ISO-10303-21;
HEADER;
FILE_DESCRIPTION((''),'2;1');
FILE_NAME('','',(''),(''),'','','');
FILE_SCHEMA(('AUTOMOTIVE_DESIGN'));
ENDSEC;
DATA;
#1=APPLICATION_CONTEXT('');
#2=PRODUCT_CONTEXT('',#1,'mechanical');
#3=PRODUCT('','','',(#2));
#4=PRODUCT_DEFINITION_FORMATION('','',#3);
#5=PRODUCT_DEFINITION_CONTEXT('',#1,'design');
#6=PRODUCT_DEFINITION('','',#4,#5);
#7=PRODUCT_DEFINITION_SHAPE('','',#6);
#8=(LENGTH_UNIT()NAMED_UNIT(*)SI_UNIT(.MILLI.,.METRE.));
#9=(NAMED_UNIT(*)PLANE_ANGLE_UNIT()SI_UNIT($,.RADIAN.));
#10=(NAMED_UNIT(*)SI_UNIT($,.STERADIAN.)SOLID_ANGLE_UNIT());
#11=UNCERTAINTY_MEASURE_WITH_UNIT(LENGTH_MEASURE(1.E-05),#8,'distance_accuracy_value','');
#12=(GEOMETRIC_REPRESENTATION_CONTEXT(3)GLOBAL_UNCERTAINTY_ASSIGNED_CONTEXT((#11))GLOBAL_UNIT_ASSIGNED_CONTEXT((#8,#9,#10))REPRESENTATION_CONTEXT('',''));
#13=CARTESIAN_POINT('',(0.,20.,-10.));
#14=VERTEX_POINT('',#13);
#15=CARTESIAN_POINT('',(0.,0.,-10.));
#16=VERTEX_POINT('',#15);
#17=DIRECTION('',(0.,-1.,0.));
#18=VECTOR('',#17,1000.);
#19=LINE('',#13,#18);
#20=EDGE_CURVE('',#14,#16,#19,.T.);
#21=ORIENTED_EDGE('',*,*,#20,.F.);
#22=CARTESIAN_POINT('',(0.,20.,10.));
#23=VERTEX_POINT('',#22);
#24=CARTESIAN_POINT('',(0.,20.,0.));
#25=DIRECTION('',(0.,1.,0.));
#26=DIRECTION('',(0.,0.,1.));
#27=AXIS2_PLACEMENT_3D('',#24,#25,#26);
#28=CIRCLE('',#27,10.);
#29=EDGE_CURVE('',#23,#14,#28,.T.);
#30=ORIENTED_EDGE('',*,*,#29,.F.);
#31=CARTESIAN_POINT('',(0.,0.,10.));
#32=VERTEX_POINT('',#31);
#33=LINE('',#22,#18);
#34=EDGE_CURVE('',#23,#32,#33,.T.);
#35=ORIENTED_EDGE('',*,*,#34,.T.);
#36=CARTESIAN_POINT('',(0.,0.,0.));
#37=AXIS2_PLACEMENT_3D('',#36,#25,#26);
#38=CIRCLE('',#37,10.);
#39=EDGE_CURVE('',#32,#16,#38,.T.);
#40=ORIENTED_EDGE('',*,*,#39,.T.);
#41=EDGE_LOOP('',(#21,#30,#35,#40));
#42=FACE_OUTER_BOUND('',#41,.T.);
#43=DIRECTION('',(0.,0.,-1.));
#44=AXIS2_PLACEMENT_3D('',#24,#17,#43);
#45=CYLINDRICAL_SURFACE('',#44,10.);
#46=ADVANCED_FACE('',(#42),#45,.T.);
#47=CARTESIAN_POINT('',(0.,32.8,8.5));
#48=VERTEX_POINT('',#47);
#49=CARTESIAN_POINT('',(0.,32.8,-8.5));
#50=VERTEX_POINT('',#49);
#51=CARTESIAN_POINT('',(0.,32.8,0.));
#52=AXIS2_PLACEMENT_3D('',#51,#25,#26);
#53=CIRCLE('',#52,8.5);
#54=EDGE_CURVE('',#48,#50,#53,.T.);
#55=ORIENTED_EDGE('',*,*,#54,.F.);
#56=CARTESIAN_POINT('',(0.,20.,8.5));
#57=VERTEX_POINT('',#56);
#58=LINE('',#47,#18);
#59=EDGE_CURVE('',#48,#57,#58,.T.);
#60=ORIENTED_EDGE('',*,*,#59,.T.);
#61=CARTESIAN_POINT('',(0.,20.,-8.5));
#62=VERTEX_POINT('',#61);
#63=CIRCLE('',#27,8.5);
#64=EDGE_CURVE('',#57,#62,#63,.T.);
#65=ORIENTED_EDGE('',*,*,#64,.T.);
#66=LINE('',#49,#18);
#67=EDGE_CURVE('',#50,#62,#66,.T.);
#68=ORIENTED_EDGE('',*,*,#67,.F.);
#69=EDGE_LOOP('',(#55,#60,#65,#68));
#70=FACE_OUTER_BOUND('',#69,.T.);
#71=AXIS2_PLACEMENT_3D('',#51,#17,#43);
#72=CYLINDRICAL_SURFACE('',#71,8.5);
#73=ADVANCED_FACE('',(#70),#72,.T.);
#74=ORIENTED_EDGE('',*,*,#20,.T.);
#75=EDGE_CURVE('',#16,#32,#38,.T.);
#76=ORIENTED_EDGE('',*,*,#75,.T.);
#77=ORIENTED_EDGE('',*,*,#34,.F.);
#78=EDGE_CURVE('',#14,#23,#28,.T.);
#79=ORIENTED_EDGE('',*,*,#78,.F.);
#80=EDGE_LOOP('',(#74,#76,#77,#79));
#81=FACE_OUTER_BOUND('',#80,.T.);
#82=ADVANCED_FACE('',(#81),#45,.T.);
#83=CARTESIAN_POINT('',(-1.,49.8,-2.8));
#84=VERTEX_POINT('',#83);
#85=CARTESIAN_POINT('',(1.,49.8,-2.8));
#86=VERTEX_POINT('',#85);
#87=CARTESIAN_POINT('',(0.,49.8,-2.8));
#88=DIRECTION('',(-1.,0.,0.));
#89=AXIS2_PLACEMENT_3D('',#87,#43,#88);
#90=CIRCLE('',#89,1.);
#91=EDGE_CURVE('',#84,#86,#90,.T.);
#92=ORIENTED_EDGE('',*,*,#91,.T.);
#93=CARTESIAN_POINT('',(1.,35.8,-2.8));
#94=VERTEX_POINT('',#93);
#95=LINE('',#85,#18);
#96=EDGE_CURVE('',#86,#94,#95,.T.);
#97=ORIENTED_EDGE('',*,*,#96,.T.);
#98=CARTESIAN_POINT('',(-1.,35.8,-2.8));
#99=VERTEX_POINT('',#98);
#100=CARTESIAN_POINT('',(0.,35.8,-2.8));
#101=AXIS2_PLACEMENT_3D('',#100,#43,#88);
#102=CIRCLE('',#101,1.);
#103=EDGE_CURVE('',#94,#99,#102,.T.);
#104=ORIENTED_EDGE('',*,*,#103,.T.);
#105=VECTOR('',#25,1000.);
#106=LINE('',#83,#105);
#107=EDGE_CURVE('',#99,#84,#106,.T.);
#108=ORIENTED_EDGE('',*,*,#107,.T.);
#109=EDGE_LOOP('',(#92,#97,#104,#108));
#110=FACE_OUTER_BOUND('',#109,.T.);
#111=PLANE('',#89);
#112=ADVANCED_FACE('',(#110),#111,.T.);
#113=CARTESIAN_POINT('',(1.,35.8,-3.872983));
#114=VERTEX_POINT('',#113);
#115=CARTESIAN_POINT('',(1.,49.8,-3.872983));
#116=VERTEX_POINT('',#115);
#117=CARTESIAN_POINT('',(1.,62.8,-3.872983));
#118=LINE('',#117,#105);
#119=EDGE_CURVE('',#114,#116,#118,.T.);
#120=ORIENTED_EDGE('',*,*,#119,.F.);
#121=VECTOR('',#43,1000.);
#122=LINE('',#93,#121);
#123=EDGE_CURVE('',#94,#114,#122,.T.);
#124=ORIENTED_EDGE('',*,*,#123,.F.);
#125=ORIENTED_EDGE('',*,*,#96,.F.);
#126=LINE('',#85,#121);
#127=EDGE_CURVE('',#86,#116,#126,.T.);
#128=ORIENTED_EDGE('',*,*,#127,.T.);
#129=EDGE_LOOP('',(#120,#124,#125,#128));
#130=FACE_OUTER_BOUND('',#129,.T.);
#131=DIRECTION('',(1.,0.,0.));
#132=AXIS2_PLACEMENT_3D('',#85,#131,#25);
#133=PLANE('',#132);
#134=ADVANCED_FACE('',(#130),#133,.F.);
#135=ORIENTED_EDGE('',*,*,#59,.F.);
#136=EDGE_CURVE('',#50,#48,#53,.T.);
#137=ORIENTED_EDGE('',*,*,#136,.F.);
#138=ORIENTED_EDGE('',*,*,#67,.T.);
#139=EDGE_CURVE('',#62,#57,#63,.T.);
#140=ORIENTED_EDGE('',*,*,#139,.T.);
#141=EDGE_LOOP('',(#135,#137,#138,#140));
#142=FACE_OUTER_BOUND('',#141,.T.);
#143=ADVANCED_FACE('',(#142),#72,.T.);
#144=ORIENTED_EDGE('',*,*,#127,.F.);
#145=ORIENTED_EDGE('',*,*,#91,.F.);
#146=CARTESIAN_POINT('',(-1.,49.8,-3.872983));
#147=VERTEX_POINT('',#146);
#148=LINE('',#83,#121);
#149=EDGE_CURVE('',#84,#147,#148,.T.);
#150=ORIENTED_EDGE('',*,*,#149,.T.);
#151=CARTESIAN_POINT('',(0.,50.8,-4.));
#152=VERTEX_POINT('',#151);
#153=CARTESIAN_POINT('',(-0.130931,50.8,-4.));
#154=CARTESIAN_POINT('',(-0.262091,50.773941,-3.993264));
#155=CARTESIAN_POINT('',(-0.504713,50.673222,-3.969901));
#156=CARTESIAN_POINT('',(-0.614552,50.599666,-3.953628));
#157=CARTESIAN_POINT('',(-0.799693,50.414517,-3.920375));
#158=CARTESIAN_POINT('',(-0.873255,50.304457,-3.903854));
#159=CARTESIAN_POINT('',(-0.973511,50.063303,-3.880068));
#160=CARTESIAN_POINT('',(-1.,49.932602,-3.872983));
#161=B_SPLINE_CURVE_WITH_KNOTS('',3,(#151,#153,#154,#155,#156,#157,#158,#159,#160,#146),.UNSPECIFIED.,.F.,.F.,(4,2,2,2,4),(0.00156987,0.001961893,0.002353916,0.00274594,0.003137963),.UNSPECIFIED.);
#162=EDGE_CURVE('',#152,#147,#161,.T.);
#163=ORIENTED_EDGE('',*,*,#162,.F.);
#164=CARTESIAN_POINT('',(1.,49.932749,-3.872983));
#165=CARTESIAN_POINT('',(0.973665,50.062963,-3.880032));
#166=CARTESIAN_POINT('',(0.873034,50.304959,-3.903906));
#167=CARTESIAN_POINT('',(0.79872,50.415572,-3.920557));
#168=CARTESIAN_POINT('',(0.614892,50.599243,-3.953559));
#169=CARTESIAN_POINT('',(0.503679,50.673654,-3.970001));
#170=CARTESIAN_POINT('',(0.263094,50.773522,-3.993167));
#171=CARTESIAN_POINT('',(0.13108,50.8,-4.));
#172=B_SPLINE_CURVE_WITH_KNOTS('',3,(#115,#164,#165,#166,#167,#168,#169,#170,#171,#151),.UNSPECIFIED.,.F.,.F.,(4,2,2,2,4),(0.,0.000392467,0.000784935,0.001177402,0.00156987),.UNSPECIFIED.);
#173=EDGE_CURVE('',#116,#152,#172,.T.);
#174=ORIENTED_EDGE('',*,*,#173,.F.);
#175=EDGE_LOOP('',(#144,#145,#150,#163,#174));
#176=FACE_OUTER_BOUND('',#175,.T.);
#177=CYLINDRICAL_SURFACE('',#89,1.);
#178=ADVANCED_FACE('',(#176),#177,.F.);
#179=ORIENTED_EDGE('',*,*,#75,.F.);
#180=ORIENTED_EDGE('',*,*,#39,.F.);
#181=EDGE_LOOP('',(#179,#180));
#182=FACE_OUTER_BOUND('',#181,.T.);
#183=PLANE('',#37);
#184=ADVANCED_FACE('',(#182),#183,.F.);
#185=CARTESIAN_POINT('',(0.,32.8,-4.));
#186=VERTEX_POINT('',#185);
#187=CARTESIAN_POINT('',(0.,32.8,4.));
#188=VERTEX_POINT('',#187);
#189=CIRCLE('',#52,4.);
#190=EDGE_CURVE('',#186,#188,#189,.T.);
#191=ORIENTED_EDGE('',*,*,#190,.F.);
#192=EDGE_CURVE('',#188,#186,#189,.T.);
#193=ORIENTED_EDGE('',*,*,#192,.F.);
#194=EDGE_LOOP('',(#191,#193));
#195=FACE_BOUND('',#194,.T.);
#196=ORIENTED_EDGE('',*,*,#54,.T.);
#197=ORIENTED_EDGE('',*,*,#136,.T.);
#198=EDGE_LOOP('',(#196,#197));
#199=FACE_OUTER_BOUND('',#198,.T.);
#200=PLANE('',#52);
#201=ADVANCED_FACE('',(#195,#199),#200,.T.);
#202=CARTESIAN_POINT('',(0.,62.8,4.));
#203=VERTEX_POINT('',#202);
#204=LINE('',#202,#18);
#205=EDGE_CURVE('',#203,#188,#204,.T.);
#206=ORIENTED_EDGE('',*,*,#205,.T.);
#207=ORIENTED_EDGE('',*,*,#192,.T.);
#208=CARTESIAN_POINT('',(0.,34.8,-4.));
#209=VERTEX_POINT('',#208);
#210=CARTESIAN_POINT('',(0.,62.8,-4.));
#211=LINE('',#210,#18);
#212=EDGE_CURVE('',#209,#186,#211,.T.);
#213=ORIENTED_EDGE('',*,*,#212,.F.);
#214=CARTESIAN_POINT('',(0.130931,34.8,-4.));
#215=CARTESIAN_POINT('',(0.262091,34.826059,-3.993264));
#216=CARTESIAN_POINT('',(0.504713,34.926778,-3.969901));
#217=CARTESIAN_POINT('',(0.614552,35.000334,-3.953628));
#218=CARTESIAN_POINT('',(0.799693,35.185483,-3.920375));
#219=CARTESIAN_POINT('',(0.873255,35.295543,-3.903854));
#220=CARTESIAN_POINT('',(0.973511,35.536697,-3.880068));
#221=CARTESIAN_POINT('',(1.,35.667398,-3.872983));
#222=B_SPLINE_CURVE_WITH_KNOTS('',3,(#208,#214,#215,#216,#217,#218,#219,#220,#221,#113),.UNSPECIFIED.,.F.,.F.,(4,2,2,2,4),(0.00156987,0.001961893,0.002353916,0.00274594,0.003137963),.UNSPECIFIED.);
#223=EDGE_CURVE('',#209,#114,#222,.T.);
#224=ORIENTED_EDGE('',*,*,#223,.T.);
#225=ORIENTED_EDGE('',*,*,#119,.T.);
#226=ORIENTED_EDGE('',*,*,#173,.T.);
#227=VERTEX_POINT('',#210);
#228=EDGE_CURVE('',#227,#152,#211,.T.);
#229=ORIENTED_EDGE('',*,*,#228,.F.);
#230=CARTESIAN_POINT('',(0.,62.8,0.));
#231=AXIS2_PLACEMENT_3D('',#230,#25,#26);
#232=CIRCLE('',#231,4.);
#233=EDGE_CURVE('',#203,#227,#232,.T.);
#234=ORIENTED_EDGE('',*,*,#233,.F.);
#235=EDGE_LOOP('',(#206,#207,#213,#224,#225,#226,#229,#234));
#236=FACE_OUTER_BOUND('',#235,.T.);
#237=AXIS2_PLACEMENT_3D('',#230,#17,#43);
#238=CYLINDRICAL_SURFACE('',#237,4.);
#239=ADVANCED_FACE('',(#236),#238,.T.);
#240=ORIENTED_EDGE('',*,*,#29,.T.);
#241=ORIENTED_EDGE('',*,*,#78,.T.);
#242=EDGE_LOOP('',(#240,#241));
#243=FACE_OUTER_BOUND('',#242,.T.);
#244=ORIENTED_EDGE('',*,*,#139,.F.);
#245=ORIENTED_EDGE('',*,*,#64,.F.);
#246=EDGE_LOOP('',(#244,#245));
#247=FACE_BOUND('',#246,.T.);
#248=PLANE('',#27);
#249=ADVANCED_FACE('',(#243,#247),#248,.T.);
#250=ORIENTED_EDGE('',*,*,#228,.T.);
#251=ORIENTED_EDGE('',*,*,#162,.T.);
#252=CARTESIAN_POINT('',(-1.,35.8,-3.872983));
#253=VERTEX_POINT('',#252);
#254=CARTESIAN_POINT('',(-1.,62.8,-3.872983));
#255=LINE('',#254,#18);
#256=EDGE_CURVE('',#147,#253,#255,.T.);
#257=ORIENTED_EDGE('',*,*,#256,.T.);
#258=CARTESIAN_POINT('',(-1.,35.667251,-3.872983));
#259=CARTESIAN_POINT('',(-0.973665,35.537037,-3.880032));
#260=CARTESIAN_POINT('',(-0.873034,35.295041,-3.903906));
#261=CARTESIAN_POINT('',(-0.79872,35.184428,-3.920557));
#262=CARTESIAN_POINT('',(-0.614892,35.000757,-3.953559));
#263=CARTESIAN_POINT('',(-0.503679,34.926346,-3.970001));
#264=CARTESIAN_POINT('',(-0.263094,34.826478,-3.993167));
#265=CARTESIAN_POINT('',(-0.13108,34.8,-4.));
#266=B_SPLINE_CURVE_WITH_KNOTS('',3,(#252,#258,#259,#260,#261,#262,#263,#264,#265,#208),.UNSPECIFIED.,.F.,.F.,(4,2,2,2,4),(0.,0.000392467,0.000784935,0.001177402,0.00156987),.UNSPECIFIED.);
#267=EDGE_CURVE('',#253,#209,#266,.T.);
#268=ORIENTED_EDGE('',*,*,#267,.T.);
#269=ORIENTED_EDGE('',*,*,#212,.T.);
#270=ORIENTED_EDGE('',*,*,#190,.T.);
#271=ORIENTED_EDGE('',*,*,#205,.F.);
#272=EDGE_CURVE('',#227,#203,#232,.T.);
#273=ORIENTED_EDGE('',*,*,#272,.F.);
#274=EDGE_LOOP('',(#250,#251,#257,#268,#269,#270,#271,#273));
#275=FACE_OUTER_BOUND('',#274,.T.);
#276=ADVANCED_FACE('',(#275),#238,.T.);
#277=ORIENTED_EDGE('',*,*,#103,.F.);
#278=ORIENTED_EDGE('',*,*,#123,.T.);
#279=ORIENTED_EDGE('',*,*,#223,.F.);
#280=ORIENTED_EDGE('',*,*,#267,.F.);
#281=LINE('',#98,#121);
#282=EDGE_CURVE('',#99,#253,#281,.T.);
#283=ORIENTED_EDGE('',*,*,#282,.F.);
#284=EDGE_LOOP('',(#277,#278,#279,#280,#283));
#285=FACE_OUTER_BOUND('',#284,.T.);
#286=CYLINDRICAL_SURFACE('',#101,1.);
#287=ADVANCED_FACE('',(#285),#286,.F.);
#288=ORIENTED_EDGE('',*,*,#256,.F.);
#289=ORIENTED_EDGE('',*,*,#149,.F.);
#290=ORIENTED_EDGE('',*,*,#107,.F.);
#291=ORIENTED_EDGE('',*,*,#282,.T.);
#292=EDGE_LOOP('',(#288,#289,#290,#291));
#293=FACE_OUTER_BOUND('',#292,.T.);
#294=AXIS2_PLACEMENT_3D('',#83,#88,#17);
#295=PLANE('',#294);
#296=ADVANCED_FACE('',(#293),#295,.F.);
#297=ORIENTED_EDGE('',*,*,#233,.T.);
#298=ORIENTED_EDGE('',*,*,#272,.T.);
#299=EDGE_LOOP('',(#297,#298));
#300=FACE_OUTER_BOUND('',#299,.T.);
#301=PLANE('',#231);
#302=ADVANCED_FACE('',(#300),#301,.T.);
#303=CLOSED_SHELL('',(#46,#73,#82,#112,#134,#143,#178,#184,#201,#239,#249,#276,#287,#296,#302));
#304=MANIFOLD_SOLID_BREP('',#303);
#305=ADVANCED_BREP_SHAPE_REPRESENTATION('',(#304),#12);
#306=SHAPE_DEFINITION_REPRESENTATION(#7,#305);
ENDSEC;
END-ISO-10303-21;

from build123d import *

# Parameters (mm, degrees)
SKETCH1_R           = 10
BOSS_EXTRUDE1_DEPTH = 20
SKETCH2_R           = 8.5
BOSS_EXTRUDE2_DEPTH = 12.8
SKETCH3_R           = 4
BOSS_EXTRUDE3_DEPTH = 30
CUT_EXTRUDE1_DEPTH  = 1.2


with BuildPart() as part:
    # Sketch1 → Boss-Extrude1 (new body)
    with BuildSketch(Plane(origin=(0, 0, 0), x_dir=(1, 0, 0), z_dir=(0, 1, 0))):
        with Locations(Location((0, 0, 0), (0, 0, 270))):
            Circle(SKETCH1_R)
    extrude(amount=BOSS_EXTRUDE1_DEPTH)

    # Sketch2 → Boss-Extrude2 (add)
    with BuildSketch(Plane(origin=(0, 20, 0), x_dir=(1, 0, 0), z_dir=(0, 1, 0))):
        with Locations(Location((0, 0, 0), (0, 0, 270))):
            Circle(SKETCH2_R)
    extrude(amount=BOSS_EXTRUDE2_DEPTH)

    # Sketch3 → Boss-Extrude3 (add)
    with BuildSketch(Plane(origin=(0, 32.8, 0), x_dir=(1, 0, 0), z_dir=(0, 1, 0))):
        with Locations(Location((0, 0, 0), (0, 0, 270))):
            Circle(SKETCH3_R)
    extrude(amount=BOSS_EXTRUDE3_DEPTH)

    # Sketch4 → Cut-Extrude1 (cut)
    with BuildSketch(Plane(origin=(0, 0, -4), x_dir=(-1, 0, 0), z_dir=(0, 0, -1))):
        with BuildLine():
            Line((1, 49.8), (1, 35.8))
            ThreePointArc((1, 35.8), (0, 34.8), (-1, 35.8))
            Line((-1, 35.8), (-1, 49.8))
            ThreePointArc((-1, 49.8), (0, 50.8), (1, 49.8))
        make_face()
    extrude(amount=-CUT_EXTRUDE1_DEPTH, mode=Mode.SUBTRACT)


solid = part.part
